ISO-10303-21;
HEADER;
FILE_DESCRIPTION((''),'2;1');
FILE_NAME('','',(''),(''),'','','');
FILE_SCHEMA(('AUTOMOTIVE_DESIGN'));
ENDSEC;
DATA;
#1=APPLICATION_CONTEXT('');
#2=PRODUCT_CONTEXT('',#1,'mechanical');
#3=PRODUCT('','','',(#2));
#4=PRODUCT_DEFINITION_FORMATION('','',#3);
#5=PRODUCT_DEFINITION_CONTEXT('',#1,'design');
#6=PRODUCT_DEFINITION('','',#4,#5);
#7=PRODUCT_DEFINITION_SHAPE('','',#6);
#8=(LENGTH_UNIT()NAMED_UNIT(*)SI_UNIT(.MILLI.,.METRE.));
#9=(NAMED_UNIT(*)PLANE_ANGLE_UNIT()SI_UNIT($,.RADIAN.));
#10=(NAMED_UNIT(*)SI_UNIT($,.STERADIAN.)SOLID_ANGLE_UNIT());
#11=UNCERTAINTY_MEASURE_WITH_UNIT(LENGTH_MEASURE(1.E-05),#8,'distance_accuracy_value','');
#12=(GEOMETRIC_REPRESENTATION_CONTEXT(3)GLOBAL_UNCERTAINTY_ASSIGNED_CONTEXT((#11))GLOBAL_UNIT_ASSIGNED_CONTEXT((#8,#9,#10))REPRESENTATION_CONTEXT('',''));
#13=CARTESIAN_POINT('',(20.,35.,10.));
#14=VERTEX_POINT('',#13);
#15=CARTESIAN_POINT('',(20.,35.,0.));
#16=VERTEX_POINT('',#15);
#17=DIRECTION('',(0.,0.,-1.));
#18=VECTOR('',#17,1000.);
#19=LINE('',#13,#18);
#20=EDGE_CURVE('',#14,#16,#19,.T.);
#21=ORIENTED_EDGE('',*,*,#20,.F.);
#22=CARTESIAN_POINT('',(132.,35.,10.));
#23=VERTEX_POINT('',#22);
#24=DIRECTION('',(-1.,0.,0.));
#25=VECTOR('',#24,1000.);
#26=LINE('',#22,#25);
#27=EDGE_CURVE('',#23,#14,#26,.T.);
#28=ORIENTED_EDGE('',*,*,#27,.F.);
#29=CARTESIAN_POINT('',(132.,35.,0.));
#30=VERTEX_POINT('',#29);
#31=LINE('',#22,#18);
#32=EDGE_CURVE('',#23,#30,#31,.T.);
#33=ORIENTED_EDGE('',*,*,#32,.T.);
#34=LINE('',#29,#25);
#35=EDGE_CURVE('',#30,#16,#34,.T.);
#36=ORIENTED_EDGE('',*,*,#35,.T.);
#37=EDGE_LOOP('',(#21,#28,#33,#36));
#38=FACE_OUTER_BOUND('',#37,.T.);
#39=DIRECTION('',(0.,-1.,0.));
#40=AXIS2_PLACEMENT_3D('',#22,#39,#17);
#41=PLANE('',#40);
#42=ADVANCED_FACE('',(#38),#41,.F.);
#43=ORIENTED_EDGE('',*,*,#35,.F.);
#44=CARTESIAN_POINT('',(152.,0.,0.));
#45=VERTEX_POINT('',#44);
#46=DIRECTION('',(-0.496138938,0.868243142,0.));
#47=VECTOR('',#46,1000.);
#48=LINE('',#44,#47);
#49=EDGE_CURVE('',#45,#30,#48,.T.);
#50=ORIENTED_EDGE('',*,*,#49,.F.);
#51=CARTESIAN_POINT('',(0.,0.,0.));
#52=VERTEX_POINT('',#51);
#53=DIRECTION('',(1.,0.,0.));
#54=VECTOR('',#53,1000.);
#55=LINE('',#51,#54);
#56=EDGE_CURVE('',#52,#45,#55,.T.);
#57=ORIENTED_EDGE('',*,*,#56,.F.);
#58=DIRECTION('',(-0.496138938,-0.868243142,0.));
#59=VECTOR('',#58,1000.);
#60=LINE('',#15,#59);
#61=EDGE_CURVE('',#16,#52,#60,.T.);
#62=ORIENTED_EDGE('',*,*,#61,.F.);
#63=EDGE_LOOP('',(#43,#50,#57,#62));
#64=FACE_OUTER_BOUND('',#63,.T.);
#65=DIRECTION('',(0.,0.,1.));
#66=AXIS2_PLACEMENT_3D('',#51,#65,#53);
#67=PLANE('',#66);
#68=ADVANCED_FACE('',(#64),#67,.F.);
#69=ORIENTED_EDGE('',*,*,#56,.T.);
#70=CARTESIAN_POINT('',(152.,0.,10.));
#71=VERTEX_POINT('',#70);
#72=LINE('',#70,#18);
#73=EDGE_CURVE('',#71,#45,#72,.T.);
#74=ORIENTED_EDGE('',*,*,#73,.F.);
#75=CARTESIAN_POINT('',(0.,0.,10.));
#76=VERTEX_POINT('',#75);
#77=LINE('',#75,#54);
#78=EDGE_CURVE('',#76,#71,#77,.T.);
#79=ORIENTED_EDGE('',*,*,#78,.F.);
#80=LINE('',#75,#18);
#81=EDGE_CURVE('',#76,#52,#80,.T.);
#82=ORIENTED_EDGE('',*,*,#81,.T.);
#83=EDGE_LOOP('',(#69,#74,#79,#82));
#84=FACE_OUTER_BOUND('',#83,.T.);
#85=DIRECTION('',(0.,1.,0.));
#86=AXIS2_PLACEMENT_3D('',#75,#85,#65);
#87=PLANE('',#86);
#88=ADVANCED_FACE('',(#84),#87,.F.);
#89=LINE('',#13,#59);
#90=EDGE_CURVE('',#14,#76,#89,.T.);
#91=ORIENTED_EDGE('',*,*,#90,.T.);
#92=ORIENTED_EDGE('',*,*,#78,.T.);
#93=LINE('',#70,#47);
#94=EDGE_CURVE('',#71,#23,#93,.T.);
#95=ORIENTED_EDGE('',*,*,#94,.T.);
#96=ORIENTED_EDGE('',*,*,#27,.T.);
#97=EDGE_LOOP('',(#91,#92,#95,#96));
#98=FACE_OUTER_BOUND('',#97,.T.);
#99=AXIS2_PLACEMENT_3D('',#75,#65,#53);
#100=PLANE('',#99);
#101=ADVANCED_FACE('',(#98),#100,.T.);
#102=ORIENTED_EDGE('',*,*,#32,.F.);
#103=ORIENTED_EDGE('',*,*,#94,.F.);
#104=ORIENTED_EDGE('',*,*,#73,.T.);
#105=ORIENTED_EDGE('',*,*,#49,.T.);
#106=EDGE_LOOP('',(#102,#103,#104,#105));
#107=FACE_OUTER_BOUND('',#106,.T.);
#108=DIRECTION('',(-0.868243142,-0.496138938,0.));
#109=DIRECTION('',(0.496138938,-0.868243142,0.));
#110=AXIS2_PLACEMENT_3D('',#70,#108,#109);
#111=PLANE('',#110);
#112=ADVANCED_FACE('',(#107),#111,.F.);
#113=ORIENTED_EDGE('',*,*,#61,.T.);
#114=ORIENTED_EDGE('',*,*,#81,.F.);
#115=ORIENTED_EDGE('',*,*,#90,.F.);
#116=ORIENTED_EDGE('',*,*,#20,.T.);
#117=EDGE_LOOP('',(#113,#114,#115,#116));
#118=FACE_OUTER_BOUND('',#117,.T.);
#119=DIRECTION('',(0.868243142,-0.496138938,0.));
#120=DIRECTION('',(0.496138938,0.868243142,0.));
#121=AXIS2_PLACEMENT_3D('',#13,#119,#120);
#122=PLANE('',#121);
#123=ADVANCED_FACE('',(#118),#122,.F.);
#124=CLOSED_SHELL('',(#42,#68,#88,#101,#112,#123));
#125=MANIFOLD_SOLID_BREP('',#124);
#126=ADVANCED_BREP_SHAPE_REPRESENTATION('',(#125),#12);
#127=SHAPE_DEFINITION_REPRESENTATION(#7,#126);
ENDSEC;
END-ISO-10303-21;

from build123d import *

# Parameters (mm, degrees)
BOSS_EXTRUDE1_DEPTH = 10


with BuildPart() as part:
    # Sketch1 → Boss-Extrude1 (new body)
    with BuildSketch(Plane.XY):
        Polygon((0, 0), (152, 0), (132, 35), (20, 35), align=None)
    extrude(amount=BOSS_EXTRUDE1_DEPTH)


solid = part.part
